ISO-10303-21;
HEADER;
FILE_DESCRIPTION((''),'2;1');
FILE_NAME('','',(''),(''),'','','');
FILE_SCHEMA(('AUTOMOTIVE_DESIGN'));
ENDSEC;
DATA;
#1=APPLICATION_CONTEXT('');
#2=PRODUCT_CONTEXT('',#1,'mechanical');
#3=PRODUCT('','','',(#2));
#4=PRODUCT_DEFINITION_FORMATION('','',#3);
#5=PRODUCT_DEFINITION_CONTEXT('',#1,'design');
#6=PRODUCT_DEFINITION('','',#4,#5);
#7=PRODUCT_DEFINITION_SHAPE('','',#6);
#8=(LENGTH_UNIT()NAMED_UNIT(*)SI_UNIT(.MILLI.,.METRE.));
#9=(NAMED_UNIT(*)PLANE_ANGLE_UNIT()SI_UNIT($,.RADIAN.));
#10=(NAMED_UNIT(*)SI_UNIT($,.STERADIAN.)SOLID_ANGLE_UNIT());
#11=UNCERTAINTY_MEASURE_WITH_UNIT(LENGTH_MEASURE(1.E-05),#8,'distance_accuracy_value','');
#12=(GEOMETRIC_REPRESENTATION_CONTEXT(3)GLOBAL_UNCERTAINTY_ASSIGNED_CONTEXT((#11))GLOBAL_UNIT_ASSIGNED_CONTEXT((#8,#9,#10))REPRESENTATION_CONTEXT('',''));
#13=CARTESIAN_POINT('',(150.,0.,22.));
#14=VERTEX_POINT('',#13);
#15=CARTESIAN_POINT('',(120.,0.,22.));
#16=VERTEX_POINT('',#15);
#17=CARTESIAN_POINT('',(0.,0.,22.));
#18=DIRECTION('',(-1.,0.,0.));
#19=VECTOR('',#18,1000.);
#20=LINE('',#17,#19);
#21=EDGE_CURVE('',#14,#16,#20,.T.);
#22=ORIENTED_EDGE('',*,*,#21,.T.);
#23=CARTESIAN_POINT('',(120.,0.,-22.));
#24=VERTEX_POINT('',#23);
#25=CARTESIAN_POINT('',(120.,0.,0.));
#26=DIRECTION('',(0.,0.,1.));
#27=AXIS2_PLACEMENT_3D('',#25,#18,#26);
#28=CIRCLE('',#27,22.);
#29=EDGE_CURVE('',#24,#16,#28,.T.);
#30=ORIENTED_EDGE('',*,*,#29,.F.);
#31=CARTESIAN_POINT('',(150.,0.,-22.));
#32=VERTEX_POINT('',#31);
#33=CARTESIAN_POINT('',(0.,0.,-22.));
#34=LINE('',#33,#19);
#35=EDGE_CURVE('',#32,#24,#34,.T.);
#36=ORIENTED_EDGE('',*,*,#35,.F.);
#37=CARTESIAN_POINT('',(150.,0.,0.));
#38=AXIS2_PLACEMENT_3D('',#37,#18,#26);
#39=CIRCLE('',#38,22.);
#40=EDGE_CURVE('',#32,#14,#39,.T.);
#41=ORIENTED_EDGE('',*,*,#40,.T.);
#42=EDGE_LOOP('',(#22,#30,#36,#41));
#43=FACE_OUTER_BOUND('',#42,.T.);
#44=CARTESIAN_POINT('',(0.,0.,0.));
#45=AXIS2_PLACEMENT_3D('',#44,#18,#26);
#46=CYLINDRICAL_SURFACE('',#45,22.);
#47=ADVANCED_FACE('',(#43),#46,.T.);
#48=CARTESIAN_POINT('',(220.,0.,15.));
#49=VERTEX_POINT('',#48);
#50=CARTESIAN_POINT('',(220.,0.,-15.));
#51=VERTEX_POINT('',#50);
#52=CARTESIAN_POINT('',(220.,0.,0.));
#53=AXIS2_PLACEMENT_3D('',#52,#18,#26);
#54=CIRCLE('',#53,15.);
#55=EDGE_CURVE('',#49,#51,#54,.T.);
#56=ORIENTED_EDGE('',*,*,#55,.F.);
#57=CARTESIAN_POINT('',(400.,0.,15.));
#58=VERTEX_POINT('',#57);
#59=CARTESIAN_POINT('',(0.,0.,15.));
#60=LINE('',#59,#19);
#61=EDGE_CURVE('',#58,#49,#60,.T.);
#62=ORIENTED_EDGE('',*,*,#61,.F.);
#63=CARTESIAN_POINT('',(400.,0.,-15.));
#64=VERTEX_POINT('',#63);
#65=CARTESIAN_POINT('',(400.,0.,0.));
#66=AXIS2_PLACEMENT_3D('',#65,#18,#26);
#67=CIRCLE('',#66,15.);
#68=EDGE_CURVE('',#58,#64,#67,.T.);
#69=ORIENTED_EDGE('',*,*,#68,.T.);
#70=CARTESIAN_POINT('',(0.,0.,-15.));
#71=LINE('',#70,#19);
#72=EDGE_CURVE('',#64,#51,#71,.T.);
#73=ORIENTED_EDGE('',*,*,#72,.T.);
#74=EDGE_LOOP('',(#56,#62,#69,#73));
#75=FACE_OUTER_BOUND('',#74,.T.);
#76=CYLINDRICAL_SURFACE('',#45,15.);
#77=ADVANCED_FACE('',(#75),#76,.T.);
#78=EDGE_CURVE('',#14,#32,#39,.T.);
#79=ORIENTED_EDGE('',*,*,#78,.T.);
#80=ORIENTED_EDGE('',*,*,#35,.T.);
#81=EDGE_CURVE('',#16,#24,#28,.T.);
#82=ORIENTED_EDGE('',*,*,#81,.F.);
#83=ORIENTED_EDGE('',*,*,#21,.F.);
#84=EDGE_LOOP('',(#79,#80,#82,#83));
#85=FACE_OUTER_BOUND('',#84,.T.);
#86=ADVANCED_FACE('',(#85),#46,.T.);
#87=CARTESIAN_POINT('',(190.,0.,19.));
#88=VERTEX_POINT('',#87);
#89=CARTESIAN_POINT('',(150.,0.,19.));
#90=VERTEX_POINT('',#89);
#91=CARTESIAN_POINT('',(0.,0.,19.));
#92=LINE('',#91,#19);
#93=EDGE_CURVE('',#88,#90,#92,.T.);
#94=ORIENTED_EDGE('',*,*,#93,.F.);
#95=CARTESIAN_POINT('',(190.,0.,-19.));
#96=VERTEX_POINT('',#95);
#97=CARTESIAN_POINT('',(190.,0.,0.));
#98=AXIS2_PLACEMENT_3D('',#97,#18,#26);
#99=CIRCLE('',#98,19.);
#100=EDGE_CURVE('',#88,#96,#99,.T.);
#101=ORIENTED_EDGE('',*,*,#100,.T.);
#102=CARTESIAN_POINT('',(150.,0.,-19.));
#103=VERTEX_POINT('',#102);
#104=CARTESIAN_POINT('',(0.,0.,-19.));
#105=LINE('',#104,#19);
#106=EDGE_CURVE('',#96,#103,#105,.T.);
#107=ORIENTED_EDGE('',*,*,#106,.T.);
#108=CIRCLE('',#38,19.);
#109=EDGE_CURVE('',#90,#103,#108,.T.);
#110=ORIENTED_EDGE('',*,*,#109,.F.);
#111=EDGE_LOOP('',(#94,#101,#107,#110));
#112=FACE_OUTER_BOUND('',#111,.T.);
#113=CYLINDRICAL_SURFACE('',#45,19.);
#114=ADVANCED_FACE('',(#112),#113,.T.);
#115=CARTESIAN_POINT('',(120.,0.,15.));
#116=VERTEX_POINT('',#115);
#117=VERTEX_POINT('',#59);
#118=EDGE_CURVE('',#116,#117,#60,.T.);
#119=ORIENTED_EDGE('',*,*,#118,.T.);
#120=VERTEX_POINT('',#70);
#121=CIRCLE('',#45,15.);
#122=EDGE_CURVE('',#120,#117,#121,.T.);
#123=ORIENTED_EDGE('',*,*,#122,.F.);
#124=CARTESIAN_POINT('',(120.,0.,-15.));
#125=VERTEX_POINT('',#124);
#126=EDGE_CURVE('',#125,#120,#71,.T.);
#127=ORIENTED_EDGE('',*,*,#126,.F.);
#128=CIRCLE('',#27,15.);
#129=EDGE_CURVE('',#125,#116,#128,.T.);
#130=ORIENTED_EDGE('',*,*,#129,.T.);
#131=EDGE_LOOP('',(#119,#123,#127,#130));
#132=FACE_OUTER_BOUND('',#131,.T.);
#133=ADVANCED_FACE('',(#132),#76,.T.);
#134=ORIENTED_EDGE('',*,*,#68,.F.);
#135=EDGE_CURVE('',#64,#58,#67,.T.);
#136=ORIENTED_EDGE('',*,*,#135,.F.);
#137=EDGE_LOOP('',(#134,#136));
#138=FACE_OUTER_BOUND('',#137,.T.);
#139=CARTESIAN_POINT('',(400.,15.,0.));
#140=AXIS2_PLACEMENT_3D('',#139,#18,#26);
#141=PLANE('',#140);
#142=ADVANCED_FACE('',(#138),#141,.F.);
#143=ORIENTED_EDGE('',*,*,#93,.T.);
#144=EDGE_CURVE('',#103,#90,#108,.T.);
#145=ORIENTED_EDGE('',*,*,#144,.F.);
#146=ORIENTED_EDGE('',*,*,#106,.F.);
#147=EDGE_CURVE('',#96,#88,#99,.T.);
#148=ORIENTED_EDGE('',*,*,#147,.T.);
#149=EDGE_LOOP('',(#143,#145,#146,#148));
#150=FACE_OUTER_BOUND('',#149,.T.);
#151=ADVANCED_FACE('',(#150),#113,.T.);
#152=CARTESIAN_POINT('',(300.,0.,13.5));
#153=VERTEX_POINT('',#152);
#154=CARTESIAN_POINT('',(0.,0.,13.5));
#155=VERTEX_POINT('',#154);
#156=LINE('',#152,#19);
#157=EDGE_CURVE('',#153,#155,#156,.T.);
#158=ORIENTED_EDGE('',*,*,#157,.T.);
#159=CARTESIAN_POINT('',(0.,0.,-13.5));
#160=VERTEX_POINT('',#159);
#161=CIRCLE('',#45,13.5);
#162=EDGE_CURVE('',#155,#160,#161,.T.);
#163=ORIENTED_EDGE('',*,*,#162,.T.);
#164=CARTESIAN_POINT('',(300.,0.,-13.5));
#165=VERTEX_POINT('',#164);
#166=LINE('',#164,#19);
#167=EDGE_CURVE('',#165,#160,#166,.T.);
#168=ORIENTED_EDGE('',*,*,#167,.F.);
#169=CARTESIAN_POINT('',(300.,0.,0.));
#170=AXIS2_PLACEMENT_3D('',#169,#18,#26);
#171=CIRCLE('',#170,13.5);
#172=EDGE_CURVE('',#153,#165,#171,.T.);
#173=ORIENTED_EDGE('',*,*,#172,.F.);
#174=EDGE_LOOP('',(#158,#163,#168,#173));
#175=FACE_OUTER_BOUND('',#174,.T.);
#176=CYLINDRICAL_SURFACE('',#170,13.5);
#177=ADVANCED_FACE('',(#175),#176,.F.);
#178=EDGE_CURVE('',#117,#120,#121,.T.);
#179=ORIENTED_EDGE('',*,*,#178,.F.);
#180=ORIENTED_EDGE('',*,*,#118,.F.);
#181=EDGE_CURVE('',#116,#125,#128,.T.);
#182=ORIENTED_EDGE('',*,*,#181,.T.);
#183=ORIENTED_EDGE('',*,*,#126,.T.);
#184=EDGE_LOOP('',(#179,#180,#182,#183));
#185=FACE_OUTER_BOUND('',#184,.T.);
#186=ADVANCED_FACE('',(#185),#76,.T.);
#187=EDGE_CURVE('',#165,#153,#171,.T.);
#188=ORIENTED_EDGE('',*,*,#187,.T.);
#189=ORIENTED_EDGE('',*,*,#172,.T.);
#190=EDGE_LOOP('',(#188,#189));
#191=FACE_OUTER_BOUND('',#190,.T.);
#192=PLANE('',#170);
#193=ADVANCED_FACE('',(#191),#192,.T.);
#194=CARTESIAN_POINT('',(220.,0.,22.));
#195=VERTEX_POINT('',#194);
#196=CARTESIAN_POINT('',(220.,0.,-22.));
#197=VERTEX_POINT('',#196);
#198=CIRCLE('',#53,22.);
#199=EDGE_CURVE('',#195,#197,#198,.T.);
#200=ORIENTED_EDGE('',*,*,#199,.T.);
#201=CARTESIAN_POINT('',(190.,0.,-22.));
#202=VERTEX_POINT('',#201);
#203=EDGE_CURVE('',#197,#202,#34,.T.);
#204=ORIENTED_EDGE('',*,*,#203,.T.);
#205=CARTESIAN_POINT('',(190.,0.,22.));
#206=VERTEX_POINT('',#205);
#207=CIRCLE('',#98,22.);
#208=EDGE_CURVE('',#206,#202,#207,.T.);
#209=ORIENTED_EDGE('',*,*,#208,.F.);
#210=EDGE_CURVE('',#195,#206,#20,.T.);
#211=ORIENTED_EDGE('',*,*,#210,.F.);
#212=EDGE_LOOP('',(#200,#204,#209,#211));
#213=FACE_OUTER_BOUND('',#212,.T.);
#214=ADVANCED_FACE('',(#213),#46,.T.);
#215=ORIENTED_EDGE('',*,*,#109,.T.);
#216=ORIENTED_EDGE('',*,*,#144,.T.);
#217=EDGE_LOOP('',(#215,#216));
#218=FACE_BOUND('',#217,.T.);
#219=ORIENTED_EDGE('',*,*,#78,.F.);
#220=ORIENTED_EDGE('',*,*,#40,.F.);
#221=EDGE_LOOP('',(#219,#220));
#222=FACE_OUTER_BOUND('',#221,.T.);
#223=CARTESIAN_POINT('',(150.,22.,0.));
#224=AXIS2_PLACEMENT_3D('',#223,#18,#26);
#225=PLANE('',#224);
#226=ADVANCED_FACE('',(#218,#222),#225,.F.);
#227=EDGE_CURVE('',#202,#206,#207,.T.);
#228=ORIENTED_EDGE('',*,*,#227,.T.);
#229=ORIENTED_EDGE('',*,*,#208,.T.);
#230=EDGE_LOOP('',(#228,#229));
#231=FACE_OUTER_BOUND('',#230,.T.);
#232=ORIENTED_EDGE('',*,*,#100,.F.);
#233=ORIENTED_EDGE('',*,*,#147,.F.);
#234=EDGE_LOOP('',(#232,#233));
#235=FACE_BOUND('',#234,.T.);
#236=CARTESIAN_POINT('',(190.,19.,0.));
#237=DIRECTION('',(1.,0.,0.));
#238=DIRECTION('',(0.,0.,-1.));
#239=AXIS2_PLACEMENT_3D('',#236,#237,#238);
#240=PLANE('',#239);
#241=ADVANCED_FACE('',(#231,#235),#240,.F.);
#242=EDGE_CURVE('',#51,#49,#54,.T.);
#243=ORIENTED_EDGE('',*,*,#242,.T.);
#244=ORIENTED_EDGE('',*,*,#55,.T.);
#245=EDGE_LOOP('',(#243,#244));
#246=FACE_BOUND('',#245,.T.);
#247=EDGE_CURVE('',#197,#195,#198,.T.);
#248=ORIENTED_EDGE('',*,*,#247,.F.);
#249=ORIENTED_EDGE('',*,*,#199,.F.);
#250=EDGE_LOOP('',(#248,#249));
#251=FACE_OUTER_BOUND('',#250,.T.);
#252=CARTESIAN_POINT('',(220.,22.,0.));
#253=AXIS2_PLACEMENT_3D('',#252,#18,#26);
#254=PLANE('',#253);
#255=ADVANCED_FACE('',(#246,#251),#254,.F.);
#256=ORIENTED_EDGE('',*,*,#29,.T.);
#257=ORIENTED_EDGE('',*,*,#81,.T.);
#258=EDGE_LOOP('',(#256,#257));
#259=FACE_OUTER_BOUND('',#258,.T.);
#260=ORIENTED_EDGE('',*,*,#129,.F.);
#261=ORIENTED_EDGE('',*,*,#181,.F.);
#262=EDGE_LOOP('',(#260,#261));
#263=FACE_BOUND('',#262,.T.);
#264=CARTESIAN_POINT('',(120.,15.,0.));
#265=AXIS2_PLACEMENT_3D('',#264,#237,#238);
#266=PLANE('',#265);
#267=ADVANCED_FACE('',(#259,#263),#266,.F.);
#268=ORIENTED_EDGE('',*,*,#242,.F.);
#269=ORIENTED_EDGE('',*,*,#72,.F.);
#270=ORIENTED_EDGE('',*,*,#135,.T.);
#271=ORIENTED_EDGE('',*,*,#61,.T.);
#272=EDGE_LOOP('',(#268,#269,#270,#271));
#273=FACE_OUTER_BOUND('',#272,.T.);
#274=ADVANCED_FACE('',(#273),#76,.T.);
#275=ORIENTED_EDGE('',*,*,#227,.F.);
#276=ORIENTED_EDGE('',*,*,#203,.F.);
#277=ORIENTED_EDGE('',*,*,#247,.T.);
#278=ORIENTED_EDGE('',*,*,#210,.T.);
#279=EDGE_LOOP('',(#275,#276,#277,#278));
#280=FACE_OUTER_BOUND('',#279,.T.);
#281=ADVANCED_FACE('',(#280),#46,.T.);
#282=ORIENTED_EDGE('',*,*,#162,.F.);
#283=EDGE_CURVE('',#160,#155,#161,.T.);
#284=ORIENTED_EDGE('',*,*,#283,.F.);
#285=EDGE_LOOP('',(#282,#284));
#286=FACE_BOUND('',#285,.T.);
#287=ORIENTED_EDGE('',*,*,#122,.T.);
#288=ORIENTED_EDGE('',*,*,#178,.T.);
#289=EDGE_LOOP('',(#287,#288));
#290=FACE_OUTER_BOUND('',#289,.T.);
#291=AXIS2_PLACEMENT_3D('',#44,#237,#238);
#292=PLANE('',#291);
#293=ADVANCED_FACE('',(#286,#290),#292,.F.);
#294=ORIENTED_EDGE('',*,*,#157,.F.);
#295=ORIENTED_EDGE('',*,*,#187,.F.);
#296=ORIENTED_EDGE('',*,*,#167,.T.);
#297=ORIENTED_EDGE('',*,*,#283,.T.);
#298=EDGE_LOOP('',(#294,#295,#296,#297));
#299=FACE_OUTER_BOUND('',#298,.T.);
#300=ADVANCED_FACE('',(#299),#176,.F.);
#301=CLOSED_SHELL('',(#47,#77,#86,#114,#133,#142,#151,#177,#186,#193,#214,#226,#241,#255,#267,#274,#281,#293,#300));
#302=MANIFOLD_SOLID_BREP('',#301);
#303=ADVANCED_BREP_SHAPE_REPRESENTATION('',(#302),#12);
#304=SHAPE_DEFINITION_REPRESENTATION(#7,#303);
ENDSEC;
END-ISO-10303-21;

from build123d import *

# Parameters (mm, degrees)
SKETCH_2_R                = 13.5
CUT_EXTRUDE_M28_1_0_DEPTH = 300


with BuildPart() as part:
    # 草图1 → 旋转1 (revolve)
    with BuildSketch(Plane.XY, mode=Mode.PRIVATE) as revolve_1_sk:
        Polygon((0, 0), (0, 15), (120, 15), (120, 22), (150, 22), (150, 19), (190, 19), (190, 22), (220, 22), (220, 15), (400, 15), (400, 0), align=None)
    revolve(revolve_1_sk.sketch.rotate(Axis((0, 0, 0), (1, 0, 0)), 90), axis=Axis((0, 0, 0), (1, 0, 0)))

    # 草图2 → 螺纹孔M28*1.0 (cut)
    with BuildSketch(Plane.ZY):
        Circle(SKETCH_2_R)
    extrude(amount=-CUT_EXTRUDE_M28_1_0_DEPTH, mode=Mode.SUBTRACT)


solid = part.part
